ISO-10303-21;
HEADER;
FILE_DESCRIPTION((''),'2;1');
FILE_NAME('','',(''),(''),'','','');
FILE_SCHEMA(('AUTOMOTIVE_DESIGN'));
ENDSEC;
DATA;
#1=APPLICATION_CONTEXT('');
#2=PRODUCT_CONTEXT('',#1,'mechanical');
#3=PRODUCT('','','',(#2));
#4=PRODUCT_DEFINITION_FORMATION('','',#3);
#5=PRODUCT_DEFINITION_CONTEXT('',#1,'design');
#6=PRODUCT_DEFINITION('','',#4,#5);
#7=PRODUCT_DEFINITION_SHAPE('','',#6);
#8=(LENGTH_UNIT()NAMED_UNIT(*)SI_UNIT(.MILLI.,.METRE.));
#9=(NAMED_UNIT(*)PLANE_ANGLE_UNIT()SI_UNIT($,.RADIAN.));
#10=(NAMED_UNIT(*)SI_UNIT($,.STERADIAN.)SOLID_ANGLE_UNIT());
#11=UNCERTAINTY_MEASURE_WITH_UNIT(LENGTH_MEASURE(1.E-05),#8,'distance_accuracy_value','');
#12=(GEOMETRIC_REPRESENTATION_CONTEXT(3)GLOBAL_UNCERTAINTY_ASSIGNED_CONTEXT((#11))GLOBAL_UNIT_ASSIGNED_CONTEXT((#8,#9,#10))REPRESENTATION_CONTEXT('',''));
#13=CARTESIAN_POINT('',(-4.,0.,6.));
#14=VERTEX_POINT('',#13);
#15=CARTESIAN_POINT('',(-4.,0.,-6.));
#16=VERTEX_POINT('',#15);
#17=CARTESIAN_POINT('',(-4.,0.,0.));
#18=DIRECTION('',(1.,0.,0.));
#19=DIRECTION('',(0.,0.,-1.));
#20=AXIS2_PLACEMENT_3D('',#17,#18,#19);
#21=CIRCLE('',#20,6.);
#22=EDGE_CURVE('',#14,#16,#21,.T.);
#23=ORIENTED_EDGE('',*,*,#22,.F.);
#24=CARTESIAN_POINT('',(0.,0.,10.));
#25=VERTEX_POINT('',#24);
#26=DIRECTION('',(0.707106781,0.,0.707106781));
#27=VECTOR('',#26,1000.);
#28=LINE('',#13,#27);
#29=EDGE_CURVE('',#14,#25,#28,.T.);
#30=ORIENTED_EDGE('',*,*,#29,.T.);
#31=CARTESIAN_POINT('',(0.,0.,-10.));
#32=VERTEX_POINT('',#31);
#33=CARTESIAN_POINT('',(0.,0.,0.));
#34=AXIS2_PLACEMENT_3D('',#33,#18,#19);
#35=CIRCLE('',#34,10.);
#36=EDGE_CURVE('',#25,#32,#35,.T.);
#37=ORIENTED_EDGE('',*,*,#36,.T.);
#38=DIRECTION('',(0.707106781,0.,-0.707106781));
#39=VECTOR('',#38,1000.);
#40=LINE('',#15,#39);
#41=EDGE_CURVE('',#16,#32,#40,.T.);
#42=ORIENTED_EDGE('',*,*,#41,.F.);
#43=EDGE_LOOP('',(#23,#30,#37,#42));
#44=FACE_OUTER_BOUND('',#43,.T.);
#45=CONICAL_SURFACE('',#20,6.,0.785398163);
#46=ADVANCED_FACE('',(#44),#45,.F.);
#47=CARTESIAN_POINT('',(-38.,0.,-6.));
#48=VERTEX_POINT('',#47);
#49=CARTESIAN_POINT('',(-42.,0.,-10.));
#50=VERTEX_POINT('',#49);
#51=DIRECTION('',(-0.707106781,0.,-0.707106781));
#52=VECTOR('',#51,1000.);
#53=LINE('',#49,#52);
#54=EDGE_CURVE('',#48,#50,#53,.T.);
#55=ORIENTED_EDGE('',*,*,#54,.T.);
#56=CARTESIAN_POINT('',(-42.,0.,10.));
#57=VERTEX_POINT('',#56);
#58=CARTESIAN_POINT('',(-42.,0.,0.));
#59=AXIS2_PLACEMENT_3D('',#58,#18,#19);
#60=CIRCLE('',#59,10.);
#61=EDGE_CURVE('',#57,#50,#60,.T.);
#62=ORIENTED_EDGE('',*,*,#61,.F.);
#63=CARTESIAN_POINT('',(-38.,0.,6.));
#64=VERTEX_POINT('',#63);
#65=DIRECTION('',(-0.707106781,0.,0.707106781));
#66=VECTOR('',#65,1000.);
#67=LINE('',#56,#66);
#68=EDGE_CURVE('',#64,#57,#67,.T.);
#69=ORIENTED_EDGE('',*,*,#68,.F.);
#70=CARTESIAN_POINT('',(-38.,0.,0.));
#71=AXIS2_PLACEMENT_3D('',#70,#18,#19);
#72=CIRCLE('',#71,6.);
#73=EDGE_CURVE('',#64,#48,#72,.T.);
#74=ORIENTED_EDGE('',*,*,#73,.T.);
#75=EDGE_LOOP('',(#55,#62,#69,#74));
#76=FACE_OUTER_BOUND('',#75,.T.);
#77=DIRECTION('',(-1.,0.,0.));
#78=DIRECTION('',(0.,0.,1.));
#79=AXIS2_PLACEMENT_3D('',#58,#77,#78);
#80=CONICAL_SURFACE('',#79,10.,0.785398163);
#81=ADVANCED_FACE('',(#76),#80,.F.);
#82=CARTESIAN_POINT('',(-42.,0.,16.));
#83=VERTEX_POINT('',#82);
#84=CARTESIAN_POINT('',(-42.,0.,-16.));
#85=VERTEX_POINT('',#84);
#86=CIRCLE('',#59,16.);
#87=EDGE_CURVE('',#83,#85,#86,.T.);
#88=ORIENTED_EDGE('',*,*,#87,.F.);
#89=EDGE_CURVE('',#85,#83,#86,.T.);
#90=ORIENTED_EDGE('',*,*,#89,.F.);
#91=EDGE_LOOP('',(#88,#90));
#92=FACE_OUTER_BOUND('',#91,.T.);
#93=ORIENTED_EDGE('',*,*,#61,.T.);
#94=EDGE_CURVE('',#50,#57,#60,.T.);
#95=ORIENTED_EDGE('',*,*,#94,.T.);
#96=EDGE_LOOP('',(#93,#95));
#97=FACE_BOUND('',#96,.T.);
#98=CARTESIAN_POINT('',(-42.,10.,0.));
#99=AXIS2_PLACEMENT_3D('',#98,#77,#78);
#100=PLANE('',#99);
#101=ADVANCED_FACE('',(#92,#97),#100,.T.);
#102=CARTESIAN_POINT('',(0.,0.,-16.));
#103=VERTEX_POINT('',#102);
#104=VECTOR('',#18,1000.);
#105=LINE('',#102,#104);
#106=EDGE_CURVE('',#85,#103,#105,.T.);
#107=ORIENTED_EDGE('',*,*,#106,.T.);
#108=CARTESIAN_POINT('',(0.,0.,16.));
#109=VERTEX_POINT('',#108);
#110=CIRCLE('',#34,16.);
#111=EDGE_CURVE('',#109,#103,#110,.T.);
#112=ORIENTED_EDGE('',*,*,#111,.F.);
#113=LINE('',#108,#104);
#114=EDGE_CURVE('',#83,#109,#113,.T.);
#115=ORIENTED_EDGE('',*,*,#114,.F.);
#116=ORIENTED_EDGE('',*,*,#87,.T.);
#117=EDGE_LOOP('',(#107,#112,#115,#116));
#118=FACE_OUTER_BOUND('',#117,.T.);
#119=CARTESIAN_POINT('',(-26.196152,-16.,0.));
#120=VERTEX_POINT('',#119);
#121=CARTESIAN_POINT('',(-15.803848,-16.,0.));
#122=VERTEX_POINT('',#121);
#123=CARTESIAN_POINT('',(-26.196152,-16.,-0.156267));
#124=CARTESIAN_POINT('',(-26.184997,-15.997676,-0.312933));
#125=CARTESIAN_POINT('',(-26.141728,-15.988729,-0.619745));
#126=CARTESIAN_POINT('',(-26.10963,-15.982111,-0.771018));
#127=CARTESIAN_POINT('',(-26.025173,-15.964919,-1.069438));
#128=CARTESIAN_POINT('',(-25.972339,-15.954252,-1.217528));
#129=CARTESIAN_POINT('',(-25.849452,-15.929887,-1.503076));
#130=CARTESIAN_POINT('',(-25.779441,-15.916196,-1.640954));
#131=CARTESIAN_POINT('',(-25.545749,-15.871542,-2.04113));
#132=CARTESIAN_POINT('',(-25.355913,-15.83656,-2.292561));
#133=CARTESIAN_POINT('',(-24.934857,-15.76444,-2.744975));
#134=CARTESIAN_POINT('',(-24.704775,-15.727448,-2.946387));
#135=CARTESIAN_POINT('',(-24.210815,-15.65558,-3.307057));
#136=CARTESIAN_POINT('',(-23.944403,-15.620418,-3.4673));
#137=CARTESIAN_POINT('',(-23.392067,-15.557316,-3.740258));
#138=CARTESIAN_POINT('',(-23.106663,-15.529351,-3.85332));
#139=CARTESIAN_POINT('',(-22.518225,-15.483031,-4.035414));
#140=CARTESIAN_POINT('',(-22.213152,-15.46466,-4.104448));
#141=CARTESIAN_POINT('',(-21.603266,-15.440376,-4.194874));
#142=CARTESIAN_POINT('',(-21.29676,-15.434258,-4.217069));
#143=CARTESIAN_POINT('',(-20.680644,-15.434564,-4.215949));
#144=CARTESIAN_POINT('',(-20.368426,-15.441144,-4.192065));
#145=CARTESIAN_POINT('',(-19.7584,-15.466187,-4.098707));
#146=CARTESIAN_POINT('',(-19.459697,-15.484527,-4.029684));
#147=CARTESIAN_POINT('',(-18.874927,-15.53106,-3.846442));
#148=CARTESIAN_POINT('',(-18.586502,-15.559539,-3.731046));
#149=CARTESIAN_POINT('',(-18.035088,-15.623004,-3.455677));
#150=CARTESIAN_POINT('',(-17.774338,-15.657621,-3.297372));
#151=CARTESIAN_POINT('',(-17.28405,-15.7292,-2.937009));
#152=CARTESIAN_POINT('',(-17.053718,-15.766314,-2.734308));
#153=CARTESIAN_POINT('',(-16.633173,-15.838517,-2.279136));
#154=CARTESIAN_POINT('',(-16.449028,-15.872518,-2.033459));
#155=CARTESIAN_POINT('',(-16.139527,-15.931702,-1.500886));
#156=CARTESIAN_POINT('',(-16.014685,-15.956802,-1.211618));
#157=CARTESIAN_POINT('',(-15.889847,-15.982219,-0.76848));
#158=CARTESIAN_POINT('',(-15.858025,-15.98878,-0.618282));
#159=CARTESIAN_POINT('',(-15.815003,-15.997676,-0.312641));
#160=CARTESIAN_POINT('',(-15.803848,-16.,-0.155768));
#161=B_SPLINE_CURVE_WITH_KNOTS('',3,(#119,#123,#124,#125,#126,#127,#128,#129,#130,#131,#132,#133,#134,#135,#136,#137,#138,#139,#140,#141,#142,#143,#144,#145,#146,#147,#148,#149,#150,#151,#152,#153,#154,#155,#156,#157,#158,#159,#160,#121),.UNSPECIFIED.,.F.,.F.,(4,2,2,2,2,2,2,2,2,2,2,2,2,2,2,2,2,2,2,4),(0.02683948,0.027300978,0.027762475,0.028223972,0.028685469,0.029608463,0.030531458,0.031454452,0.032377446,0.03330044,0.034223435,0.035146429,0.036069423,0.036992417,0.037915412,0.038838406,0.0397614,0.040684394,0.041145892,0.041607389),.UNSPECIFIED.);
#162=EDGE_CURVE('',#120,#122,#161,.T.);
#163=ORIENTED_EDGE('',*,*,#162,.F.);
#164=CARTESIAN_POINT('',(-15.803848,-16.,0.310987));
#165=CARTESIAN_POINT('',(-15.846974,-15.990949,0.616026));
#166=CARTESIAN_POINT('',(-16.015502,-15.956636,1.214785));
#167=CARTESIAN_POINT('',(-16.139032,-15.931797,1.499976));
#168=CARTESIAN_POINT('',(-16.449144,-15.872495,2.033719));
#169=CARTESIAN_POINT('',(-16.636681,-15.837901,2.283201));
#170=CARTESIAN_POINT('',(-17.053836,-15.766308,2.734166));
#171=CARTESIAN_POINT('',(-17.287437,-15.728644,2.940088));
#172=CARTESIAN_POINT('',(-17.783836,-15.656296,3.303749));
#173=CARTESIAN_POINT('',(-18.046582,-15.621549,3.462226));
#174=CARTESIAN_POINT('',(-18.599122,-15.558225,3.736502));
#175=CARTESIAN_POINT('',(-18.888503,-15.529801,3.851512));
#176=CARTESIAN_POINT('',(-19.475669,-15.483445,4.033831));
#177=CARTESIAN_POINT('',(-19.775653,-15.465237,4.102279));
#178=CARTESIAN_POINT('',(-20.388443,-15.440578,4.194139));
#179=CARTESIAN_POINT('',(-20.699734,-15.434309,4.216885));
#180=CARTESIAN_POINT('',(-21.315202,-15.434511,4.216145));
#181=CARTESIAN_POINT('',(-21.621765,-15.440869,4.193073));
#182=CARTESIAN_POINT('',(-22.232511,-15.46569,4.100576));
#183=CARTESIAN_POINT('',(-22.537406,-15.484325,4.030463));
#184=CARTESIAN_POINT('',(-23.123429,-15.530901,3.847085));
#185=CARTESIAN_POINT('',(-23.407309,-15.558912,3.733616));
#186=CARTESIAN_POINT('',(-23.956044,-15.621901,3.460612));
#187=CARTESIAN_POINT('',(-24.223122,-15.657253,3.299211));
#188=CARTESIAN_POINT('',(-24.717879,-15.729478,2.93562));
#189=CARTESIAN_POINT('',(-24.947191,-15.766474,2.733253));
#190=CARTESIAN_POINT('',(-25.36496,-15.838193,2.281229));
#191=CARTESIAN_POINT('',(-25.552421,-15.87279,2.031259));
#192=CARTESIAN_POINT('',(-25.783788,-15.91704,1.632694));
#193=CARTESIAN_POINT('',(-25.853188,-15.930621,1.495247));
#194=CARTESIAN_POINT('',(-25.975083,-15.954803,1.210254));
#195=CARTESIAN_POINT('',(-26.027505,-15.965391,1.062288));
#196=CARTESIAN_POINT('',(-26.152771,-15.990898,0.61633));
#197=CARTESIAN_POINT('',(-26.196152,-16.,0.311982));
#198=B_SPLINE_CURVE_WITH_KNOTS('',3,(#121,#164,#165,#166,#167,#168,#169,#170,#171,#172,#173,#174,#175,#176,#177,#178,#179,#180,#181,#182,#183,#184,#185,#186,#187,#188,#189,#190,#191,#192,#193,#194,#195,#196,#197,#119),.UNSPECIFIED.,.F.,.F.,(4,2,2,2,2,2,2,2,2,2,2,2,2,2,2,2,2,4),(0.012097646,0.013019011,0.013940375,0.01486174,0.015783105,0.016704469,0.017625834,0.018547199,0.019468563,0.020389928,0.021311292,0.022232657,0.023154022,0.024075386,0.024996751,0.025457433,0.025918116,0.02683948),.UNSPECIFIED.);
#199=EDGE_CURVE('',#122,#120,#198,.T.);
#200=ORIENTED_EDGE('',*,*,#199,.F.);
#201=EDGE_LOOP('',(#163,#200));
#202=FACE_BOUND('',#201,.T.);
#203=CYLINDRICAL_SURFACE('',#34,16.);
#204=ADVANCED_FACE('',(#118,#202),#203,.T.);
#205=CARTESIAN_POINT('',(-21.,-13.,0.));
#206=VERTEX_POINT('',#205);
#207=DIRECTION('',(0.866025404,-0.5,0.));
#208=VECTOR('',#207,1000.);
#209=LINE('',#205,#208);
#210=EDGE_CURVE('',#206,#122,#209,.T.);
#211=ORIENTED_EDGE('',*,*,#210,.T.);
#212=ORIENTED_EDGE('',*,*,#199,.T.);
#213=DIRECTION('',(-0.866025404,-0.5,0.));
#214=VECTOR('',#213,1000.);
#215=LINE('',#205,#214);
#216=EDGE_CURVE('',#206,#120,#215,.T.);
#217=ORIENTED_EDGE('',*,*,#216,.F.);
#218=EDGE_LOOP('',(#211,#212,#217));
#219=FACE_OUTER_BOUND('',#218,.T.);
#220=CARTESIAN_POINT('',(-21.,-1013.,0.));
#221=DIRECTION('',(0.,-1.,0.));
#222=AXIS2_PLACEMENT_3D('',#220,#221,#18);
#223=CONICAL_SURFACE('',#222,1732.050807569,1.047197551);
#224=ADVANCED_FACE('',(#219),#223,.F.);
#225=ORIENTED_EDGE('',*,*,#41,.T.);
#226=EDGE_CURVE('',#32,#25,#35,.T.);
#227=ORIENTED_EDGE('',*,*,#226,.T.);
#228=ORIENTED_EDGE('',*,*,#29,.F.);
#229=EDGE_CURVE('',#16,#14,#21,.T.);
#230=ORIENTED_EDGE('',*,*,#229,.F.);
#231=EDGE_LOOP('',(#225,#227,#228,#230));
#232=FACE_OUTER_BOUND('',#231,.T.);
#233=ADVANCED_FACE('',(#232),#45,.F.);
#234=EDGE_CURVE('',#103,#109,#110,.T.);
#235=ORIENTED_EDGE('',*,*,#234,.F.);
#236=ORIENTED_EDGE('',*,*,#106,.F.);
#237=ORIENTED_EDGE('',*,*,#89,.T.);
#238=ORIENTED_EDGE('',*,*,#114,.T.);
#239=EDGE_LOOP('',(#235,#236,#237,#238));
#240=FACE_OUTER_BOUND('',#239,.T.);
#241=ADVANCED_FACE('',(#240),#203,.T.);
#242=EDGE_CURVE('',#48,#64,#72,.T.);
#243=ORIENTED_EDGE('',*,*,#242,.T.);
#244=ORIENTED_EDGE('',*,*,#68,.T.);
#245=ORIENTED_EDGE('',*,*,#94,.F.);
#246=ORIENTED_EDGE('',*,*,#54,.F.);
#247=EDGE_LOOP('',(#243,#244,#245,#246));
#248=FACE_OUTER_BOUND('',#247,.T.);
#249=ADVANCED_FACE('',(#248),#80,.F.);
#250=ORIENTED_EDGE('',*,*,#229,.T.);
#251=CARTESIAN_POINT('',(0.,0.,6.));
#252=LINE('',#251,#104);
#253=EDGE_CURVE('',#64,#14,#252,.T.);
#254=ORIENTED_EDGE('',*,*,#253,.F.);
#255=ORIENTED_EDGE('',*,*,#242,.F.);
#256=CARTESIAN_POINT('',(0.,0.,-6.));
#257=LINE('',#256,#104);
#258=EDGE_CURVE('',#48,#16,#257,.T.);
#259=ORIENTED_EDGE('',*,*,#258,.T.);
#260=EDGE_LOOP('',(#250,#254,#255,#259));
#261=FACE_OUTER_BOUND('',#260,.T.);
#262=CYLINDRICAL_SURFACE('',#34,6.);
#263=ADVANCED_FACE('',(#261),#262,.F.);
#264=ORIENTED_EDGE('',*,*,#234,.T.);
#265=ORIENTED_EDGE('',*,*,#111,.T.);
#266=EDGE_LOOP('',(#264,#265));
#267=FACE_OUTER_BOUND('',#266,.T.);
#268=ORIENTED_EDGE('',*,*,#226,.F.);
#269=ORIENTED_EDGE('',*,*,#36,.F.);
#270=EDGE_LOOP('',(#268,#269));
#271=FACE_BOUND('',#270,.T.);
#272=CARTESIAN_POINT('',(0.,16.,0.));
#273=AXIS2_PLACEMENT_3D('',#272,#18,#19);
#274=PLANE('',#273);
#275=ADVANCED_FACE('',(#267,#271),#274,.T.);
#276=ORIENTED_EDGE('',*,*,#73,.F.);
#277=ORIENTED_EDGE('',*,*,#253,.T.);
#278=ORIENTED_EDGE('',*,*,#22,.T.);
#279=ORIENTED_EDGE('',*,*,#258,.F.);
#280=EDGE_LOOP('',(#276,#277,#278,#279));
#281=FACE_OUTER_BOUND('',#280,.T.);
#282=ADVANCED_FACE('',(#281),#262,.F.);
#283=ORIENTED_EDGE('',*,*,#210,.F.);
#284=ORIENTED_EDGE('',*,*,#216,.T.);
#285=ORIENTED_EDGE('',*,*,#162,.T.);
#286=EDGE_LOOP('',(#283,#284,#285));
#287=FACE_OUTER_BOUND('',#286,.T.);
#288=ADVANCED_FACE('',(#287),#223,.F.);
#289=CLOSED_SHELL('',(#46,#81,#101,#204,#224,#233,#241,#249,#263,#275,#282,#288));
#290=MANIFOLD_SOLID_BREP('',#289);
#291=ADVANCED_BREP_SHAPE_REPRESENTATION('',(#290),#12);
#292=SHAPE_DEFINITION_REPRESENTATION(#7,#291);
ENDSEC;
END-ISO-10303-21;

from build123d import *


with BuildPart() as part:
    # Bush Profile Sketch → Bush Body (revolve)
    with BuildSketch(Plane.XY, mode=Mode.PRIVATE) as bush_body_sk:
        Polygon((0, 10), (-4, 6), (-38, 6), (-42, 10), (-42, 16), (0, 16), align=None)
    revolve(bush_body_sk.sketch.rotate(Axis((0, 0, 0), (-1, 0, 0)), 90), axis=Axis((0, 0, 0), (-1, 0, 0)))

    # Internal Cut Profile Sketch → Internal Revolved Cut (revolve, cut)
    with BuildSketch(Plane.XY, mode=Mode.PRIVATE) as internal_revolved_cut_sk:
        Polygon((-26.196152423, -16), (-21, -13), (-21, -16), align=None)
    revolve(internal_revolved_cut_sk.sketch.rotate(Axis((-21, 0, 0), (0, -1, 0)), 180), axis=Axis((-21, 0, 0), (0, -1, 0)), mode=Mode.SUBTRACT)


solid = part.part
